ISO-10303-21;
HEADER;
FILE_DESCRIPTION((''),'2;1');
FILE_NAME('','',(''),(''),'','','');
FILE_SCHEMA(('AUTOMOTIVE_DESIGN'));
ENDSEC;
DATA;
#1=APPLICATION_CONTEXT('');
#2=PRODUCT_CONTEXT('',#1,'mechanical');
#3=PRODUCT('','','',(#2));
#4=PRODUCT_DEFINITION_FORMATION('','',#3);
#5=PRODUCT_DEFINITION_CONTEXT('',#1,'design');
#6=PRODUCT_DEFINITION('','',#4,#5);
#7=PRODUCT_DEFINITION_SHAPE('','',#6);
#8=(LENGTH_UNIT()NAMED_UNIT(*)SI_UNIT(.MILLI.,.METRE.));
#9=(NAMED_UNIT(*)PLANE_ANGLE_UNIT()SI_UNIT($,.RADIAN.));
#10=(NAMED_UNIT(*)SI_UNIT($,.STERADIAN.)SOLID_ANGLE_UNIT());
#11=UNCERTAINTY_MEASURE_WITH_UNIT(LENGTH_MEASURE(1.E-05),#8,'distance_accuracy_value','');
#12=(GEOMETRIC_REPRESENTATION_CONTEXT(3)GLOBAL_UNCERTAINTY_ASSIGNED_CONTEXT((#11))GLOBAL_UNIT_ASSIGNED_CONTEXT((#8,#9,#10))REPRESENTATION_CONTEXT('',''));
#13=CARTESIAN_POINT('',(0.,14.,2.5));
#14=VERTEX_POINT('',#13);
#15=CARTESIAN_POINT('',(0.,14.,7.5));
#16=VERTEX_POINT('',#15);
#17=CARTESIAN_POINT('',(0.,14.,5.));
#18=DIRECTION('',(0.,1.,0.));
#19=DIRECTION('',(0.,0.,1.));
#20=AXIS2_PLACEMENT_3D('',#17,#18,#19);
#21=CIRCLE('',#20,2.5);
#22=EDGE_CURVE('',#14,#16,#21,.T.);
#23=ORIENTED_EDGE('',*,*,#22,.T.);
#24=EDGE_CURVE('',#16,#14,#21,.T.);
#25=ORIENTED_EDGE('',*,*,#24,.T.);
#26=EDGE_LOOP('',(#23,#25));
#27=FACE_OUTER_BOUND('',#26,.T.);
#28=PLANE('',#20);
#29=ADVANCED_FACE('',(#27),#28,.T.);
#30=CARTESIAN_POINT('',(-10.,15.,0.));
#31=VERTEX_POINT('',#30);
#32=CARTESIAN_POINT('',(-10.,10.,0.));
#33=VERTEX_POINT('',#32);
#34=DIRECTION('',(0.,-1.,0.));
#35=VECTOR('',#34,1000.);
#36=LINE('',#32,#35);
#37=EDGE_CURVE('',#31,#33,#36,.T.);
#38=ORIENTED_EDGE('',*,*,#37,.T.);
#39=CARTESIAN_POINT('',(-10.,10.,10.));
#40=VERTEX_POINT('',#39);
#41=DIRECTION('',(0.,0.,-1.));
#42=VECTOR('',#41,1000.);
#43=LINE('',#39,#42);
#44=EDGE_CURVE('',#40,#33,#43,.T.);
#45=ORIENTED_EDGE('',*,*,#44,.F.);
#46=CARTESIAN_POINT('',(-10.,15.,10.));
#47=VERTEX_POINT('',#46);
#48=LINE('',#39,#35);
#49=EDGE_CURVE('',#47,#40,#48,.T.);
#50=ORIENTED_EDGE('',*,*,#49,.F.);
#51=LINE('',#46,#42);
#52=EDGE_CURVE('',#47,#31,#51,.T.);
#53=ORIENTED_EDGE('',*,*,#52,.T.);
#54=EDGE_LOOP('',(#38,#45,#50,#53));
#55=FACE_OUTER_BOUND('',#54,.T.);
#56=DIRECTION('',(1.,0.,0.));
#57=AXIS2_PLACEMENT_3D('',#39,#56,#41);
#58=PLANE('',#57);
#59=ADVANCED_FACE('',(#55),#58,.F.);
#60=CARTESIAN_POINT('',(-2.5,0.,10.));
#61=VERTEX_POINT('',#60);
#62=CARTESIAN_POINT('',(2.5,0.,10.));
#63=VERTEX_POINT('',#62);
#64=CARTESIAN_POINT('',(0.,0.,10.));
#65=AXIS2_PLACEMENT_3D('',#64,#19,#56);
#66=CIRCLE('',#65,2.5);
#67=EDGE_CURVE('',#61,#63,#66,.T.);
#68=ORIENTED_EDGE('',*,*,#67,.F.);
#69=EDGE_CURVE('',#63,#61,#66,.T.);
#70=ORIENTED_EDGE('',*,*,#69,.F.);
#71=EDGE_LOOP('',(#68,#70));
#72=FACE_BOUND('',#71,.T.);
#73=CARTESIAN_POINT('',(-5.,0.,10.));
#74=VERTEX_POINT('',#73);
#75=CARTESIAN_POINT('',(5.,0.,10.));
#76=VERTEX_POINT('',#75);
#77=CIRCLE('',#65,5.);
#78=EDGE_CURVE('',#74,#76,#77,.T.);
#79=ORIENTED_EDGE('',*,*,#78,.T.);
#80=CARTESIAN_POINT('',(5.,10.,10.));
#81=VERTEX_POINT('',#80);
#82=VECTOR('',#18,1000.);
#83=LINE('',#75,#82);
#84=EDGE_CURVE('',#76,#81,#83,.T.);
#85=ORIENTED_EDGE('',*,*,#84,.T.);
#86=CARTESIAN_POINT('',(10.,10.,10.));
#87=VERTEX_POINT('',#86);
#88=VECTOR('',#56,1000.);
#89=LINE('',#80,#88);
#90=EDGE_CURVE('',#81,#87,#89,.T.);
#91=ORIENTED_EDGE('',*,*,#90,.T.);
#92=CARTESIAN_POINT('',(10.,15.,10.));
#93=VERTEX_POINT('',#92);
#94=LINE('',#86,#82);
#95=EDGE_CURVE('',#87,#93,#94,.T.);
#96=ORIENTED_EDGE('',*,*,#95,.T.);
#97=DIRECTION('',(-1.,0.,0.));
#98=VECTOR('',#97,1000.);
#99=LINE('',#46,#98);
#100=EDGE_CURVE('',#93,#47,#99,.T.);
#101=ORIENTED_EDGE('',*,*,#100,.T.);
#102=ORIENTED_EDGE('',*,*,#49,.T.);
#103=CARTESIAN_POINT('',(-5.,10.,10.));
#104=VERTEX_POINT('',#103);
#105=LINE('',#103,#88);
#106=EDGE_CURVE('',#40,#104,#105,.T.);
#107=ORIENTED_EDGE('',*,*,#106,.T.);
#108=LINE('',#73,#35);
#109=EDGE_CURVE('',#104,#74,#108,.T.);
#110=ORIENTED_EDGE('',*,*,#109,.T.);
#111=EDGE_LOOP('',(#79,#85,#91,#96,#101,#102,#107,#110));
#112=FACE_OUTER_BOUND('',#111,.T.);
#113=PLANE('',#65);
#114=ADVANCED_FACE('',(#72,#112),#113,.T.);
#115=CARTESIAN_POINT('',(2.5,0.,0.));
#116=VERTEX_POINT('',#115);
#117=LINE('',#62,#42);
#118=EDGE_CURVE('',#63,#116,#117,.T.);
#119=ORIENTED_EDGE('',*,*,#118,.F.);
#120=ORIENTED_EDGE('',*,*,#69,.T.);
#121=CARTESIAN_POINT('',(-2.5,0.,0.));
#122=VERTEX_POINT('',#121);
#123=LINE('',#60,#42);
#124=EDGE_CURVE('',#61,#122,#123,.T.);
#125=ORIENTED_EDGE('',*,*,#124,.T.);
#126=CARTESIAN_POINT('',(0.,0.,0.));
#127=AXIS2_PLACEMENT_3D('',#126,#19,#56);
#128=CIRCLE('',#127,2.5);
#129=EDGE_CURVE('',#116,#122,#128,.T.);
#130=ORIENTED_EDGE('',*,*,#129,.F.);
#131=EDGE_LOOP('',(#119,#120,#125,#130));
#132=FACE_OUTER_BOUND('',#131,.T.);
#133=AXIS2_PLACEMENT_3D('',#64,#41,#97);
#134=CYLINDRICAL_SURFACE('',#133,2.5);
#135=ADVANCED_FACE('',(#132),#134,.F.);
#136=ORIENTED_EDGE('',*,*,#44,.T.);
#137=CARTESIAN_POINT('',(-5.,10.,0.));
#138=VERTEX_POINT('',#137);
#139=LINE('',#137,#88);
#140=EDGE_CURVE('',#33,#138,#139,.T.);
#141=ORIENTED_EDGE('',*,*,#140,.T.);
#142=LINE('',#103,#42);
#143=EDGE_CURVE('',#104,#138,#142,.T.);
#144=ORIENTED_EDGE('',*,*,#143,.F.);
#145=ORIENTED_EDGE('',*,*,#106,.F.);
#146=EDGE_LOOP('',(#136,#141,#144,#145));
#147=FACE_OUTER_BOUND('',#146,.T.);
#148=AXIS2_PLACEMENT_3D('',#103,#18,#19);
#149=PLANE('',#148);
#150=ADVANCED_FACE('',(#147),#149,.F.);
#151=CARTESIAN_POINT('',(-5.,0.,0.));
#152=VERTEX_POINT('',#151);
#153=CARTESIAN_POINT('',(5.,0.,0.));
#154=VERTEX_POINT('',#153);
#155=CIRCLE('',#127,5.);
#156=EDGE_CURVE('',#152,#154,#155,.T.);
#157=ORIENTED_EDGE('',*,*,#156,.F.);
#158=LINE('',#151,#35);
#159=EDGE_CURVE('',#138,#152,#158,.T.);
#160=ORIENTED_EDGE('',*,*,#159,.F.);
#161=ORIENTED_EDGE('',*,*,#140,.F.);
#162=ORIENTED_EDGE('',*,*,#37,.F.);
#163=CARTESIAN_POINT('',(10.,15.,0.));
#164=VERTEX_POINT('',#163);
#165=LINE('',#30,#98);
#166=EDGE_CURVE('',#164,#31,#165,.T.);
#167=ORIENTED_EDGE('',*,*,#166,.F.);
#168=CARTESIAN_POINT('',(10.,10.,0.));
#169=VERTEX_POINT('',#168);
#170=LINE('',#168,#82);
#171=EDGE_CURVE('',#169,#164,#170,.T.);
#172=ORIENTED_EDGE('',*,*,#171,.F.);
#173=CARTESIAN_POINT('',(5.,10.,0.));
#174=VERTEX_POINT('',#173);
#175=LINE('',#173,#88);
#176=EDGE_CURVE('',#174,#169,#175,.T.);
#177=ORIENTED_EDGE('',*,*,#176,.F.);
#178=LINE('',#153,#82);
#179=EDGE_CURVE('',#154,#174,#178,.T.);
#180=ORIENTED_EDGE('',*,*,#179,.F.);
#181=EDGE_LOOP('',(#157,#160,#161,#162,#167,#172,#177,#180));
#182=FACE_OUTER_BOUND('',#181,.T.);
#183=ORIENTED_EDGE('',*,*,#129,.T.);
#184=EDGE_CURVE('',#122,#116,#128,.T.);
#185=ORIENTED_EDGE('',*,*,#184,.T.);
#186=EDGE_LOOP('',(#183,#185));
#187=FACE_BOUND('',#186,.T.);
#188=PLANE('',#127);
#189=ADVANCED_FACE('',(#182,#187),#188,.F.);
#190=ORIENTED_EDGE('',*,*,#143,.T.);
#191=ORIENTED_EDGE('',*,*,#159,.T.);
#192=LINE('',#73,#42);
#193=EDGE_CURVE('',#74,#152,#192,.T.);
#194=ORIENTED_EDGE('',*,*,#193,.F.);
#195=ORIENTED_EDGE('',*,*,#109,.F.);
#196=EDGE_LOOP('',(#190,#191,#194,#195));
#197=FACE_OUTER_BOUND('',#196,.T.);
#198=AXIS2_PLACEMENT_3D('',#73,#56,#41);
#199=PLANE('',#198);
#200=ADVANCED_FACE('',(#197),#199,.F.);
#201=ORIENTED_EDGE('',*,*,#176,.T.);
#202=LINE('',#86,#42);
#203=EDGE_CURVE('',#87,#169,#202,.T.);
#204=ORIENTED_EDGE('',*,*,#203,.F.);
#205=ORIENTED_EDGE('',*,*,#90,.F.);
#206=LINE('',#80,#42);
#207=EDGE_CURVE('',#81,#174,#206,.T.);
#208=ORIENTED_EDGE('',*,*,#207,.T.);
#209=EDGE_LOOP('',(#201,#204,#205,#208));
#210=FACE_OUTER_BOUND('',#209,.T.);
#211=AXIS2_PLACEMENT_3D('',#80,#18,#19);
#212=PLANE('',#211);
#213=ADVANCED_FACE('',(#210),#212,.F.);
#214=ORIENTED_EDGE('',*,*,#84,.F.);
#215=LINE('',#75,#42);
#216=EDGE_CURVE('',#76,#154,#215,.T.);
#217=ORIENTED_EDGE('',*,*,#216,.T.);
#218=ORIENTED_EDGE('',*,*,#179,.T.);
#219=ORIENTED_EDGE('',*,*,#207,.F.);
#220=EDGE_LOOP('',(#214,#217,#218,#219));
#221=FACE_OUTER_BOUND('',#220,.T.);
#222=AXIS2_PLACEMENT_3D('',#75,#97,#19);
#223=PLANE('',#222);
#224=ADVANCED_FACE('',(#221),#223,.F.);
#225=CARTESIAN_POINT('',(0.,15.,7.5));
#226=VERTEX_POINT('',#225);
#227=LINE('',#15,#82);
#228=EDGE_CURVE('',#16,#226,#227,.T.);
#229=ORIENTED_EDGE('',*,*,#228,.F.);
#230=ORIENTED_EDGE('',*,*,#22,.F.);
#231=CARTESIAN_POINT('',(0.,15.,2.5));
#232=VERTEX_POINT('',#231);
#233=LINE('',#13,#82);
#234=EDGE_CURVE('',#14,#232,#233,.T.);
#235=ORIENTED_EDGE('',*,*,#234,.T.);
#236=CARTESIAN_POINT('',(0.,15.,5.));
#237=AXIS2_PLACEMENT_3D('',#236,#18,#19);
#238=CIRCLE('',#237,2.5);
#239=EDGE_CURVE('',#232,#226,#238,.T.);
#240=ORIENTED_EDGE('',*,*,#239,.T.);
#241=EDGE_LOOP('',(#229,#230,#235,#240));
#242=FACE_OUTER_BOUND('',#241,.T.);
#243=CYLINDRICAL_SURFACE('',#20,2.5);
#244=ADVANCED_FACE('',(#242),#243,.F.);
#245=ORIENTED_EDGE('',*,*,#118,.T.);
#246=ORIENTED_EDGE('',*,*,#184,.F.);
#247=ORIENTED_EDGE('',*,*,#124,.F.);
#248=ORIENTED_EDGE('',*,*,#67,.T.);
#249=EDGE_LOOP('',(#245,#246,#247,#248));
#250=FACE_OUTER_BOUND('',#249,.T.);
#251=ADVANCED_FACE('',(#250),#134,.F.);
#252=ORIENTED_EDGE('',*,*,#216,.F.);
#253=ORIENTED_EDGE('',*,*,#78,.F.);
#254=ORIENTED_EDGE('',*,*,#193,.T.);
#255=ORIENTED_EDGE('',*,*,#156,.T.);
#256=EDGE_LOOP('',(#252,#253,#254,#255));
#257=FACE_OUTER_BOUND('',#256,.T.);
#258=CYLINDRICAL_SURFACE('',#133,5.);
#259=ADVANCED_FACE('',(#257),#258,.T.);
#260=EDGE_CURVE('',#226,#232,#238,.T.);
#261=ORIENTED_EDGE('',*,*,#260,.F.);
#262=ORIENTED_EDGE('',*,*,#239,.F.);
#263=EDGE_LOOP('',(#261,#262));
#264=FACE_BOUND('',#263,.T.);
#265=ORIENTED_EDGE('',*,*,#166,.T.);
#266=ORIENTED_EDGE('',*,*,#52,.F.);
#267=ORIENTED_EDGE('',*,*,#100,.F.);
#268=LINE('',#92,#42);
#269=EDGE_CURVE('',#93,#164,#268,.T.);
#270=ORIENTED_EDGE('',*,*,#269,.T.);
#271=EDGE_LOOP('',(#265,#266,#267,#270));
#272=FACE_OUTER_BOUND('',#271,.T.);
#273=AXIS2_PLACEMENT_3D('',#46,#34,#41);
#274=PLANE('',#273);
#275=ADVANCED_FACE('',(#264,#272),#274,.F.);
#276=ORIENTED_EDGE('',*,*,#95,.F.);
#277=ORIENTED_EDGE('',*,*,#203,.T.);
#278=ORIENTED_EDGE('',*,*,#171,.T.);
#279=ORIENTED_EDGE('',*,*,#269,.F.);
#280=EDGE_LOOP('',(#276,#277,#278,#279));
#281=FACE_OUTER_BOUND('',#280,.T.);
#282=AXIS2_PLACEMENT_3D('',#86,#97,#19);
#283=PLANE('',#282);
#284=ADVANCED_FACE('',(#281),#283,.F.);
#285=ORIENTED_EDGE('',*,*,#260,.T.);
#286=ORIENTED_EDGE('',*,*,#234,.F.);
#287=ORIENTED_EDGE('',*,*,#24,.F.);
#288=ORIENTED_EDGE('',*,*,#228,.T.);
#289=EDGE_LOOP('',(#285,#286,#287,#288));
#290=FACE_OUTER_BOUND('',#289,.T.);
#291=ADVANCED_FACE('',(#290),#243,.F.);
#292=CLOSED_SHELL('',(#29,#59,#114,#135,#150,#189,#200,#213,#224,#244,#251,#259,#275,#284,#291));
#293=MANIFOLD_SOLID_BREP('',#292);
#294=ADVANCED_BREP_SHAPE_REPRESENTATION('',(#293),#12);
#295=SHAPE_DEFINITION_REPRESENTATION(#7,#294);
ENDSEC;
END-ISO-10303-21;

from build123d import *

# Parameters (mm, degrees)
SKETCH1_R           = 2.5
BOSS_EXTRUDE1_DEPTH = 10
SKETCH2_R           = 2.5
CUT_EXTRUDE1_DEPTH  = 1


with BuildPart() as part:
    # Sketch1 → Boss-Extrude1 (new body)
    with BuildSketch(Plane.XY):
        with BuildLine():
            Line((-5, 0), (-5, 10))
            Line((-5, 10), (-10, 10))
            Line((-10, 10), (-10, 15))
            Line((-10, 15), (10, 15))
            Line((10, 15), (10, 10))
            Line((10, 10), (5, 10))
            Line((5, 10), (5, 0))
            ThreePointArc((5, 0), (0, -5), (-5, 0))
        make_face()
        Circle(SKETCH1_R, mode=Mode.SUBTRACT)
    extrude(amount=BOSS_EXTRUDE1_DEPTH)

    # Sketch2 → Cut-Extrude1 (cut)
    with BuildSketch(Plane(origin=(0, 15, 0), x_dir=(1, 0, 0), z_dir=(0, 1, 0))):
        with Locations(Location((0, -5, 0), (0, 0, 270))):
            Circle(SKETCH2_R)
    extrude(amount=-CUT_EXTRUDE1_DEPTH, mode=Mode.SUBTRACT)


solid = part.part
